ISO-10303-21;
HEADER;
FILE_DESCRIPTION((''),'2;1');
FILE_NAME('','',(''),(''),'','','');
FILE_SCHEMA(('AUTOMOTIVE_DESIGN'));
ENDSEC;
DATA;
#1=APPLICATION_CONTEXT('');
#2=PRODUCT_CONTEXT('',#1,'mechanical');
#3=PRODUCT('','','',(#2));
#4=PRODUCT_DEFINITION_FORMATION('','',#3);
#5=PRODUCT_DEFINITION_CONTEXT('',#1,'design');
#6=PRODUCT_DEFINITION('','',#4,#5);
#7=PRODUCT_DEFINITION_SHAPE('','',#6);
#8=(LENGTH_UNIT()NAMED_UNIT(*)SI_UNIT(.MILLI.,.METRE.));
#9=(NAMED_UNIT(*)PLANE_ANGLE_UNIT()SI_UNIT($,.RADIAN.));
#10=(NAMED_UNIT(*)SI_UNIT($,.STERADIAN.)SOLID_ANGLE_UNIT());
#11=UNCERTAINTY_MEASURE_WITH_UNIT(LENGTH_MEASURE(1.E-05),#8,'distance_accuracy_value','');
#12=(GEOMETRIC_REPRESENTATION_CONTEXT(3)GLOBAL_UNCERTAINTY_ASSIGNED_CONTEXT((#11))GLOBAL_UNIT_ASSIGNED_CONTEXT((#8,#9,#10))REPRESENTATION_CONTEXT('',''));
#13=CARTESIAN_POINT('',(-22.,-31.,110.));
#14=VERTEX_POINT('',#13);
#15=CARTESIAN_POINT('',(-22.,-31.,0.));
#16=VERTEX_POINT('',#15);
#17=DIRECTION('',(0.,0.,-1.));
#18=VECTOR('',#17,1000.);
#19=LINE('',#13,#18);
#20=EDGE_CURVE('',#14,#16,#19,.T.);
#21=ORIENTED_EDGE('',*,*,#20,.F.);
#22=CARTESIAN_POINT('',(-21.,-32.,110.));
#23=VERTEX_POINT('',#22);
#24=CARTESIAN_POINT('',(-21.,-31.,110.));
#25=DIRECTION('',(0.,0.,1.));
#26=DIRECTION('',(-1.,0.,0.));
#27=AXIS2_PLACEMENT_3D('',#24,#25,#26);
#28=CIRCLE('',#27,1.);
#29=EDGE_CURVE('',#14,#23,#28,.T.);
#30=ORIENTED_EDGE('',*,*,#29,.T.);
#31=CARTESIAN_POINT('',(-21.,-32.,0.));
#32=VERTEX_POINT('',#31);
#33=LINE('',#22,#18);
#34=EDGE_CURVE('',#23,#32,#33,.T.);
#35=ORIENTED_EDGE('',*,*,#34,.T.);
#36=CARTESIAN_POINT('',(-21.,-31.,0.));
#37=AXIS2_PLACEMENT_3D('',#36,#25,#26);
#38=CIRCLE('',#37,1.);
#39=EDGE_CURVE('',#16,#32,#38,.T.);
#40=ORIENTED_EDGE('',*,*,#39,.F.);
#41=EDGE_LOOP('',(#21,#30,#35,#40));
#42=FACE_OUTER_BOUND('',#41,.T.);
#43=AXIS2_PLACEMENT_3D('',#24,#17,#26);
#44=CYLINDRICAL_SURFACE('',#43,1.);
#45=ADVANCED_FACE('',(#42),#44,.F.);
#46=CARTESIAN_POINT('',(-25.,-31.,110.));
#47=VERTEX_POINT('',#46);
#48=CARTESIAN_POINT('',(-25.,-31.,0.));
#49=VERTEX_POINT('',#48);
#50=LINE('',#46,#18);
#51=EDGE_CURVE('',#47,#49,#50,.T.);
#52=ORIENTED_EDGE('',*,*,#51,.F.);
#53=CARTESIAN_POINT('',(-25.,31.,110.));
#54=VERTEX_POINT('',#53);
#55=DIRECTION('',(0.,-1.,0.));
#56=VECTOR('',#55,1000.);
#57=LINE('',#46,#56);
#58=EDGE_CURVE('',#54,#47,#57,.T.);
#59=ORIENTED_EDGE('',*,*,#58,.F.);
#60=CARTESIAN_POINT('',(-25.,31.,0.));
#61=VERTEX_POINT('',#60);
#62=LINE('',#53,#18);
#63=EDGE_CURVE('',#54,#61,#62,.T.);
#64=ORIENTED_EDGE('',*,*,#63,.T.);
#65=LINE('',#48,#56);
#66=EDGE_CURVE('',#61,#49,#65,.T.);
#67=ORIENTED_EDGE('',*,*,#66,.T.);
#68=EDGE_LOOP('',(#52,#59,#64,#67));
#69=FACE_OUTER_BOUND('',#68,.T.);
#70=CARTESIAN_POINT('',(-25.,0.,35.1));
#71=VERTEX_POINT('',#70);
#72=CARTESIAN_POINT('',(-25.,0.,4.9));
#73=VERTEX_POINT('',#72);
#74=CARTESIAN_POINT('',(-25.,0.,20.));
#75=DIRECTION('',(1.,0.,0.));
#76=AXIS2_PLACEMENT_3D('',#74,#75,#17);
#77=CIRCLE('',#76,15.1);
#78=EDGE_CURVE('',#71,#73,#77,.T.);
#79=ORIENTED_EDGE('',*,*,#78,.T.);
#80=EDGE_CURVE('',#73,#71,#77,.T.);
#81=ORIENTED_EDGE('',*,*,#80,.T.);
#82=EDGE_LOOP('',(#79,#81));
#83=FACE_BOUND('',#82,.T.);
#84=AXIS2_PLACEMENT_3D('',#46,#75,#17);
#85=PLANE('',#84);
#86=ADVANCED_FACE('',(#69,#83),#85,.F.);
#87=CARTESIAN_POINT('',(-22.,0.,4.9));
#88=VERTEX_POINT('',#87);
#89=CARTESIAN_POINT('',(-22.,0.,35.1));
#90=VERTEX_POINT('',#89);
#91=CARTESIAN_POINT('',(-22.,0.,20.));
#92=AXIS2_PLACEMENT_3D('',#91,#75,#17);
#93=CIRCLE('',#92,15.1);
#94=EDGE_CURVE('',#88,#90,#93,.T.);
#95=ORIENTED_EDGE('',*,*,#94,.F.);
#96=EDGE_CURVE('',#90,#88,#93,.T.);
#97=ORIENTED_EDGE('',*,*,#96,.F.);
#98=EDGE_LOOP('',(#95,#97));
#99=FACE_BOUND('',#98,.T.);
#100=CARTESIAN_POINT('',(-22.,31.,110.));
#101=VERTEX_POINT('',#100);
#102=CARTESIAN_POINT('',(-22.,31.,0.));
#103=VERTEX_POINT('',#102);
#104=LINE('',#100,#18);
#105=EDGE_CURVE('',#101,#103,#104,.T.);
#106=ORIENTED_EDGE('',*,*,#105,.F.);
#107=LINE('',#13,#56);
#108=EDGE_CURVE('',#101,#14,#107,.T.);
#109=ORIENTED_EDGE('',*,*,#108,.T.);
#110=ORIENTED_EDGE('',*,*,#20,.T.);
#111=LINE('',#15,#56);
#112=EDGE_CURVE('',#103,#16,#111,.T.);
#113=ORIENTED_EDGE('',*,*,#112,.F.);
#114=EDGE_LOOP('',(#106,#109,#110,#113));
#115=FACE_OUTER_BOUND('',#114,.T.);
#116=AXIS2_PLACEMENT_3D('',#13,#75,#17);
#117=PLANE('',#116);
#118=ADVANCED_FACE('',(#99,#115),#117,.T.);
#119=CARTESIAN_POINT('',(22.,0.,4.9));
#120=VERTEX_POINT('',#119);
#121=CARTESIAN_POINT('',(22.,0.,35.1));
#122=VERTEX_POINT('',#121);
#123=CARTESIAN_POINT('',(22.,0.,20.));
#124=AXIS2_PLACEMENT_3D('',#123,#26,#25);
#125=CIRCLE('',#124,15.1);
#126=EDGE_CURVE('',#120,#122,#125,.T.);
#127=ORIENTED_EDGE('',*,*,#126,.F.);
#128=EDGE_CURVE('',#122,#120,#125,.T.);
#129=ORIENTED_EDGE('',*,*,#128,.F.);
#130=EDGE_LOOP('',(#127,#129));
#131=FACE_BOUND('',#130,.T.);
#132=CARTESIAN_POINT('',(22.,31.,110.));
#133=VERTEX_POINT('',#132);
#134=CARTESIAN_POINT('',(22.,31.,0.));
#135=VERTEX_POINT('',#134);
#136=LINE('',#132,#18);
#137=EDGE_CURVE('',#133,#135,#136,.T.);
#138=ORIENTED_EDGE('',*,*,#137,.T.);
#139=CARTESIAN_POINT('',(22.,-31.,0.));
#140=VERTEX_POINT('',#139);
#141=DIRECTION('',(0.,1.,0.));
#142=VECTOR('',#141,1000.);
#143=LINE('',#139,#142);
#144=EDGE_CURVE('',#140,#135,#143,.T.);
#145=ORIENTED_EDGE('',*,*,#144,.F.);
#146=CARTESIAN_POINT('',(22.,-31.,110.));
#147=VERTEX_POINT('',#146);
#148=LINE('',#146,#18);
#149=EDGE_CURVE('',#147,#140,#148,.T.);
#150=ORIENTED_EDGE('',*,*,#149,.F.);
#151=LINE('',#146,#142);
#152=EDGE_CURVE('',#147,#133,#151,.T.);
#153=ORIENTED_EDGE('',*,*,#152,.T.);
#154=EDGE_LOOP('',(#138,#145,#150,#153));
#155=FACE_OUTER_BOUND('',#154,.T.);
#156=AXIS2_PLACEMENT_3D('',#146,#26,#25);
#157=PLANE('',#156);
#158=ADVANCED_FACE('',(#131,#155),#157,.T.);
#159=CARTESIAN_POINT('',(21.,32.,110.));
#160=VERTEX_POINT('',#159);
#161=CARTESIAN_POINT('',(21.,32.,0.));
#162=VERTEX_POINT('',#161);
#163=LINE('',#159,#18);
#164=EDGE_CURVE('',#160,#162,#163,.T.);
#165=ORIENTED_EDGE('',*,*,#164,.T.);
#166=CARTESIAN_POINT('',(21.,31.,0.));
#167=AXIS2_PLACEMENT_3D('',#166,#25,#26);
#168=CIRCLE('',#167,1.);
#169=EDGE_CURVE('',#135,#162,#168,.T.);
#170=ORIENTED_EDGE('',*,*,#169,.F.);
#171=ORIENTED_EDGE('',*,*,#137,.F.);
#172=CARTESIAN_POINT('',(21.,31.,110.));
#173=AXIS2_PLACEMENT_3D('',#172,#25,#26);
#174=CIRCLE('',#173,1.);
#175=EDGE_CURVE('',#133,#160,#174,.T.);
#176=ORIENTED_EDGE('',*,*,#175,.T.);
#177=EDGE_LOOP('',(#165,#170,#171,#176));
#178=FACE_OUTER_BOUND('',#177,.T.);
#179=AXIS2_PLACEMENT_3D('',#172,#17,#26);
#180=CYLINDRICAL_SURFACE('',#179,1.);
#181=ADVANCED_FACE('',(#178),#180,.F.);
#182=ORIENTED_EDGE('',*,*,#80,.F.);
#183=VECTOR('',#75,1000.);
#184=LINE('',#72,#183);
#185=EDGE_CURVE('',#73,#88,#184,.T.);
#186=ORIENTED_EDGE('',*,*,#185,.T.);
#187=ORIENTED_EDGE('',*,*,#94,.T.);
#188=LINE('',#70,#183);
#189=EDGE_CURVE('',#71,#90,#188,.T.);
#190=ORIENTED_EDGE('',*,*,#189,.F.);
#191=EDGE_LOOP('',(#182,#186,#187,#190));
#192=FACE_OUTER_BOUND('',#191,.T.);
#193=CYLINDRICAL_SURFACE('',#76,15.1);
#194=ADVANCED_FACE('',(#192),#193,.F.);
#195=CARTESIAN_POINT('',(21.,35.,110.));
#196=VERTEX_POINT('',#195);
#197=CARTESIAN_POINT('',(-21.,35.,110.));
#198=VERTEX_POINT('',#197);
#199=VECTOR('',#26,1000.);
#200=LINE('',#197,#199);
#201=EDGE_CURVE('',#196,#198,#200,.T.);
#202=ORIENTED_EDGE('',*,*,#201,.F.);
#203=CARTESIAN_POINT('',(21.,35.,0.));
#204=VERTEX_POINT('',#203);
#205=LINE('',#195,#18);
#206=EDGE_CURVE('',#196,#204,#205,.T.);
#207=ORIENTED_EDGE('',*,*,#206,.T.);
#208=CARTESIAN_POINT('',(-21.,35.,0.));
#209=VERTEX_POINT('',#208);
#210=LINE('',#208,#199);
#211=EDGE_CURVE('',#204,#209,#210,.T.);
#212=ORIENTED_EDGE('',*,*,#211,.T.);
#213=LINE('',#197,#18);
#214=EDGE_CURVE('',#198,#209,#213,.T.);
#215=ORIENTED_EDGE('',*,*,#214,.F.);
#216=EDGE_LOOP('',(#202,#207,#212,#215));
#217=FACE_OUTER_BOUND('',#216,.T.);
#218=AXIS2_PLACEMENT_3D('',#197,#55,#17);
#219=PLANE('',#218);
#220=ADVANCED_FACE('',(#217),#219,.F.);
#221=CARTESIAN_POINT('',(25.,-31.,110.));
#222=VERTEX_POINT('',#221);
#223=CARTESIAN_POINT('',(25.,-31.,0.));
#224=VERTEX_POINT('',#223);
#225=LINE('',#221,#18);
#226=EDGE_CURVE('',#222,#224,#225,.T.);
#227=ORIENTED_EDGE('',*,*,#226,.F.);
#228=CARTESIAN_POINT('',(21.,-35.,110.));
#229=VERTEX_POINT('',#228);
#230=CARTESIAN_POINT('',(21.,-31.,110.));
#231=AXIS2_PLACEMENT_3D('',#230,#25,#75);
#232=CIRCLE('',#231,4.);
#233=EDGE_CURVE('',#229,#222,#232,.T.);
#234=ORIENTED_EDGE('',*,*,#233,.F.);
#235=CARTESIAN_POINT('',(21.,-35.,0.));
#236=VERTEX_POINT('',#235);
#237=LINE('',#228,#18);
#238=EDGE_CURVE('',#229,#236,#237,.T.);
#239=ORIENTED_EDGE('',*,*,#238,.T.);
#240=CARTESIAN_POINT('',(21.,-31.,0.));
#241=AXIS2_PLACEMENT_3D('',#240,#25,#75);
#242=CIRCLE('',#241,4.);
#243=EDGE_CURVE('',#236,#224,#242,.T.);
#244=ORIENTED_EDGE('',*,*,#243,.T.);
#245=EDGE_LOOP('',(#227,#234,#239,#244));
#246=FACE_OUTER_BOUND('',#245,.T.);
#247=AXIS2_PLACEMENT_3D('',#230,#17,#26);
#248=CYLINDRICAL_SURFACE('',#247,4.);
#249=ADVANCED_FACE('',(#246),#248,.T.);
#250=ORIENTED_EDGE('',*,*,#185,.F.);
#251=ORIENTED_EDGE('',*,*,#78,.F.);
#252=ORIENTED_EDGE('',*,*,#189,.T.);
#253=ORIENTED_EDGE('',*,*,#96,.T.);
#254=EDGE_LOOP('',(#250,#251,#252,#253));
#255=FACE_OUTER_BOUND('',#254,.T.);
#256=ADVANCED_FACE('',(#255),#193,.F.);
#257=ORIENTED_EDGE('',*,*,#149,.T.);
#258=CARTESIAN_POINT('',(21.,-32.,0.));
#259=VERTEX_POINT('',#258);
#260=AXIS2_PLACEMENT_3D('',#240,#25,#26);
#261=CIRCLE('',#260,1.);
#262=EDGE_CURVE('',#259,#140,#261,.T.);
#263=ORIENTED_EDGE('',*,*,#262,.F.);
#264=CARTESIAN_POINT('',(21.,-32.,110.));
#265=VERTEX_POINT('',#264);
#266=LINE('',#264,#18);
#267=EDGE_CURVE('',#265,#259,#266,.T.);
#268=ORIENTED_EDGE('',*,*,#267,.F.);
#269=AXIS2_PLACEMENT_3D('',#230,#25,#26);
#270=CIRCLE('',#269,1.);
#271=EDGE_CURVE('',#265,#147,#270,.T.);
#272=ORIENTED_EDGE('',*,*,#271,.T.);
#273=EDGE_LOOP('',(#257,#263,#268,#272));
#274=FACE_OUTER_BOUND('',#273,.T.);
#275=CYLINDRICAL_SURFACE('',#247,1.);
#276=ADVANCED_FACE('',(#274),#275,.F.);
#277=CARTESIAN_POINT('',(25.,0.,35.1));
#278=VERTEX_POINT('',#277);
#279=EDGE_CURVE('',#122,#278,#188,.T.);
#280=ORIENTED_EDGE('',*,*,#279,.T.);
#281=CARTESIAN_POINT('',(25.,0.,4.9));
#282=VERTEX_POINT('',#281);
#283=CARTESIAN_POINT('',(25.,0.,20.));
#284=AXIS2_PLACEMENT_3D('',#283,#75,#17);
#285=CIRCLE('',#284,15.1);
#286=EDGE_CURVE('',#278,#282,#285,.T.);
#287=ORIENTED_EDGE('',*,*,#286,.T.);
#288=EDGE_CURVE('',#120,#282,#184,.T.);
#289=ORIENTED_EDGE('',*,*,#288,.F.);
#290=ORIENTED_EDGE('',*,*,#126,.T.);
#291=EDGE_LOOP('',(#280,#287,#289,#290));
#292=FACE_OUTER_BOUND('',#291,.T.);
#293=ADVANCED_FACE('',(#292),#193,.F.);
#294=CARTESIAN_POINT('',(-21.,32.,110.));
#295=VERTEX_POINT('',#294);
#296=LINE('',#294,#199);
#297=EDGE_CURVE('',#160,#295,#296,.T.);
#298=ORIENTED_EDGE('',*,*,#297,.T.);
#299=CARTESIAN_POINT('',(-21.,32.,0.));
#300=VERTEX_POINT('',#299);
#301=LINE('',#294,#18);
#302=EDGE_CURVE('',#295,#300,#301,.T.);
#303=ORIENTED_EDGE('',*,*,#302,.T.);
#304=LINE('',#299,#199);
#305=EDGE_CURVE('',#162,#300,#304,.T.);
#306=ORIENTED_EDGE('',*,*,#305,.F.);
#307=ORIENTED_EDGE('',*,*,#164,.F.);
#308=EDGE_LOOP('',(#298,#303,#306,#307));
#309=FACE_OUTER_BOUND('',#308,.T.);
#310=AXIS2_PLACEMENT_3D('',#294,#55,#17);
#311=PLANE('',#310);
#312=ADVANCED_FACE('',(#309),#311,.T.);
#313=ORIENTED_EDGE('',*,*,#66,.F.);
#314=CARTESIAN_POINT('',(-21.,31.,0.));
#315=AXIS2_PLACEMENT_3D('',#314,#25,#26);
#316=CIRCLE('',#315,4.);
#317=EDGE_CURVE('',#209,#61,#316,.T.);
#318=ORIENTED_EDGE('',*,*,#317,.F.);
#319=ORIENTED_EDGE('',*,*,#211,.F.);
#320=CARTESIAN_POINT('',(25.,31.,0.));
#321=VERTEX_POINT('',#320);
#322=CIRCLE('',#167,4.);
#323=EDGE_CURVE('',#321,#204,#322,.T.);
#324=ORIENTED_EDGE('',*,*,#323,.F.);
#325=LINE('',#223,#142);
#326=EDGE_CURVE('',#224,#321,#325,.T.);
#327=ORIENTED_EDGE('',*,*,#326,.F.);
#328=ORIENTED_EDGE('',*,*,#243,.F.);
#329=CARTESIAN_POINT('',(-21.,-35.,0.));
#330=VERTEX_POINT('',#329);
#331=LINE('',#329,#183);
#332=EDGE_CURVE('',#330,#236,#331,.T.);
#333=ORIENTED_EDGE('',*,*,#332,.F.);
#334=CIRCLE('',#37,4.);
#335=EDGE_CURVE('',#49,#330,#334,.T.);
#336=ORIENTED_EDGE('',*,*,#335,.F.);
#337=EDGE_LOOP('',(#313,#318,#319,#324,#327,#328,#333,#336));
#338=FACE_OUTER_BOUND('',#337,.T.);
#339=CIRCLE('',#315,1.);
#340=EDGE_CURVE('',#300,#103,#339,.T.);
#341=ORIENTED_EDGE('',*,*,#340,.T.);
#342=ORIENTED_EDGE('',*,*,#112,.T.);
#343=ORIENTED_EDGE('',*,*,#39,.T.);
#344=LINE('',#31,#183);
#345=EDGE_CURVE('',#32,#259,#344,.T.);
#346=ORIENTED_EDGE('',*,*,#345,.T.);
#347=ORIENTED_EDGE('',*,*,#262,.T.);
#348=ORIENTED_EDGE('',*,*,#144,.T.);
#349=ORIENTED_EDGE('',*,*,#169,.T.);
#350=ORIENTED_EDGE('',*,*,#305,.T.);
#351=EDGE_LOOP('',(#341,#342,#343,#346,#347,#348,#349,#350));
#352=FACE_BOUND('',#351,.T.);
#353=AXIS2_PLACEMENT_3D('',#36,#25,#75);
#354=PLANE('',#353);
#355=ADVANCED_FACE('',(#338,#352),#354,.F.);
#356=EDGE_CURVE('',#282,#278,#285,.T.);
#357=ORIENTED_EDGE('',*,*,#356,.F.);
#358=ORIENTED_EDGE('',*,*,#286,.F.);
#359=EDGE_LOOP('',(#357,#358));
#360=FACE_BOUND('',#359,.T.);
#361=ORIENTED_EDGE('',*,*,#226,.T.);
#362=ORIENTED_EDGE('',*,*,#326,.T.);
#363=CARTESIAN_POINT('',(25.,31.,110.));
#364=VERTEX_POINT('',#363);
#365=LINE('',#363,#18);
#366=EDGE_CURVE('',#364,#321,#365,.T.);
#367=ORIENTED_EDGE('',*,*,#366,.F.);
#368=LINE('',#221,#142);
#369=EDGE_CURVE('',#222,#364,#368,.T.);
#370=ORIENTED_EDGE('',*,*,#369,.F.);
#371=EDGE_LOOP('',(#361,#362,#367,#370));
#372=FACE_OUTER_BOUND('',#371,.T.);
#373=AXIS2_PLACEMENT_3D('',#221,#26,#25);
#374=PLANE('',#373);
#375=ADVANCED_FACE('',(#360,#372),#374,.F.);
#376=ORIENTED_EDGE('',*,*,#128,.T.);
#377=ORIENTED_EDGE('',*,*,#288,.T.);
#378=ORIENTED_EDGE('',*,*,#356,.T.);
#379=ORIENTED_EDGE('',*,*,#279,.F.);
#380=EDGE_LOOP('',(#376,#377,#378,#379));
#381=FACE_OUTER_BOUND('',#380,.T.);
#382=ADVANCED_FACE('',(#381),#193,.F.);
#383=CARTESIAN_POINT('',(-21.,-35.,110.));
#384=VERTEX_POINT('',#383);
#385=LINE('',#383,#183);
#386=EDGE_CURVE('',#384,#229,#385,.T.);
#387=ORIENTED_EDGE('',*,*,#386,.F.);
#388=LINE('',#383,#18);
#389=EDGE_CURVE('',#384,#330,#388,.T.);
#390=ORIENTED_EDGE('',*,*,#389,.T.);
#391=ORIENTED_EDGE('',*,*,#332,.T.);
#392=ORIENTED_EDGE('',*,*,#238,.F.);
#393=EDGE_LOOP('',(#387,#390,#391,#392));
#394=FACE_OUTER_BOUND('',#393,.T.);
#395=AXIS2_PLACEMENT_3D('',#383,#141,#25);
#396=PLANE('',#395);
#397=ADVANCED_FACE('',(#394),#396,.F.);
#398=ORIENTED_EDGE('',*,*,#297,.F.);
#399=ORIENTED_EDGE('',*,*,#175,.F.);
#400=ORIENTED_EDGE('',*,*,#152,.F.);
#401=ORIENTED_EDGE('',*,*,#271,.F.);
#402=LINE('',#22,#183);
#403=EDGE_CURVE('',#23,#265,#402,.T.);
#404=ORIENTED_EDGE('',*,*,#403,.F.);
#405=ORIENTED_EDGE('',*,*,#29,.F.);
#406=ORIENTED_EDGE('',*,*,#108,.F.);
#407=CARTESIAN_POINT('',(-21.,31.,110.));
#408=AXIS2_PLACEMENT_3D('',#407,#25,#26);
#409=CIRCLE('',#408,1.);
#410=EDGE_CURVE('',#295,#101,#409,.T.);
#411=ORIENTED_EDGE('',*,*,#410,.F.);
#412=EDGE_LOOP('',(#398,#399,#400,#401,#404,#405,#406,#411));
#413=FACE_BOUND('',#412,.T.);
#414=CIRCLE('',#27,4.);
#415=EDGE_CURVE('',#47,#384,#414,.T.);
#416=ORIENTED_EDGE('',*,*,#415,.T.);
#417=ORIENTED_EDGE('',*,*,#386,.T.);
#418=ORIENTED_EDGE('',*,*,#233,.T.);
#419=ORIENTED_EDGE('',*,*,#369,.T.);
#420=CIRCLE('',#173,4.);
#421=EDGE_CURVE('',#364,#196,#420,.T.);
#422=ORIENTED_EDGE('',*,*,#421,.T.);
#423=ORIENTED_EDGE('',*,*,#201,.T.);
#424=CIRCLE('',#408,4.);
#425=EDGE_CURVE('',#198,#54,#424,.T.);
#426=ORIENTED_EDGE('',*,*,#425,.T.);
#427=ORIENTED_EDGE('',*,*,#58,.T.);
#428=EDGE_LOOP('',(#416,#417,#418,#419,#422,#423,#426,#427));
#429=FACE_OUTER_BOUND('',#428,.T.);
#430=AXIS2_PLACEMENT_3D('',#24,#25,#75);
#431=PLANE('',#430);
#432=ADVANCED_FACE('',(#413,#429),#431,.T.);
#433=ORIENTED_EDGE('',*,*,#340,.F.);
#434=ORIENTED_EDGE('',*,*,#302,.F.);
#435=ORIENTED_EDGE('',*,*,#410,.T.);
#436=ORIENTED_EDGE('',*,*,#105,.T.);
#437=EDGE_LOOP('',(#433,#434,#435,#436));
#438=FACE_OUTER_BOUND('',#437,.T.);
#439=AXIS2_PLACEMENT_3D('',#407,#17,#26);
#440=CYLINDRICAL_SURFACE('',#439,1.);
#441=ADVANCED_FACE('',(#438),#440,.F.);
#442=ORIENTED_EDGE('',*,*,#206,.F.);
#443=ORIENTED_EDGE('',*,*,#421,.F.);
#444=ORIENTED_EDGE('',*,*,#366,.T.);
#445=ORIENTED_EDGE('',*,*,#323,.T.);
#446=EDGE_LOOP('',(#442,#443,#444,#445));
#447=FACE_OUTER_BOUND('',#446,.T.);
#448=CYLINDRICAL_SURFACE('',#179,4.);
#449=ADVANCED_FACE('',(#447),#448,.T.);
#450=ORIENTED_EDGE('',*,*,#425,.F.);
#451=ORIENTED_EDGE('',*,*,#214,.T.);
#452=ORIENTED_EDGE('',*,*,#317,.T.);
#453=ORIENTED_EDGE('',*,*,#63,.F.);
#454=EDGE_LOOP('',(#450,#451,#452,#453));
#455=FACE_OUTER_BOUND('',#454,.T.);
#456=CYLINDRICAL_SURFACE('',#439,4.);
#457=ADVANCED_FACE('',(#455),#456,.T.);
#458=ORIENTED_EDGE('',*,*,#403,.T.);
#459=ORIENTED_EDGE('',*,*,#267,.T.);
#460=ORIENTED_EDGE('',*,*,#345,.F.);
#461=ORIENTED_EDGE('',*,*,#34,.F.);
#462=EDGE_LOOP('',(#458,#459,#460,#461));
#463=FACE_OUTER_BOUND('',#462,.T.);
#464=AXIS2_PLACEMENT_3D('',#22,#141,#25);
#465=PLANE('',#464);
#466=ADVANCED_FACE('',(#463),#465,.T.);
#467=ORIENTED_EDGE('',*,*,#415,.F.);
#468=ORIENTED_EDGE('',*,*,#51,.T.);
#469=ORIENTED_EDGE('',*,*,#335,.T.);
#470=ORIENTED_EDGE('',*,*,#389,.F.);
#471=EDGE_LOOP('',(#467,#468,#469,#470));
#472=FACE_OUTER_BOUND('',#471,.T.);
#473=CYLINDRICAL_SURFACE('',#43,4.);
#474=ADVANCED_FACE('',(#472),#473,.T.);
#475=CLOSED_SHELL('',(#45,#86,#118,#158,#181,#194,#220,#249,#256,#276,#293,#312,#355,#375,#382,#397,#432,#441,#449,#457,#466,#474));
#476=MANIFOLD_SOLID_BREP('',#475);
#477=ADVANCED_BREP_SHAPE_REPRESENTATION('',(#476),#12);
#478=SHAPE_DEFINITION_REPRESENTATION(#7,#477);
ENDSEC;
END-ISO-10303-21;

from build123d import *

# Parameters (mm, degrees)
EXTRUDE_THIN1_DEPTH = 110
SKETCH2_R           = 15.1
CUT_EXTRUDE1_DEPTH  = 126.797456254


with BuildPart() as part:
    # Sketch1 → Extrude-Thin1 (new body)
    with BuildSketch(Plane.XY):
        with BuildLine():
            Line((-25, 31), (-25, -31))
            ThreePointArc((-25, -31), (-23.828427125, -33.828427125), (-21, -35))
            Line((-21, -35), (21, -35))
            ThreePointArc((21, -35), (23.828427125, -33.828427125), (25, -31))
            Line((25, -31), (25, 31))
            ThreePointArc((25, 31), (23.828427125, 33.828427125), (21, 35))
            Line((21, 35), (-21, 35))
            ThreePointArc((-21, 35), (-23.828427125, 33.828427125), (-25, 31))
        make_face()
        with BuildLine():
            Line((-22, 31), (-22, -31))
            ThreePointArc((-22, -31), (-21.707106781, -31.707106781), (-21, -32))
            Line((-21, -32), (21, -32))
            ThreePointArc((21, -32), (21.707106781, -31.707106781), (22, -31))
            Line((22, -31), (22, 31))
            ThreePointArc((22, 31), (21.707106781, 31.707106781), (21, 32))
            Line((21, 32), (-21, 32))
            ThreePointArc((-21, 32), (-21.707106781, 31.707106781), (-22, 31))
        make_face(mode=Mode.SUBTRACT)
    extrude(amount=EXTRUDE_THIN1_DEPTH)

    # Sketch2 → Cut-Extrude1 (cut, through all)
    with BuildSketch(Plane(origin=(25, 0, 0), x_dir=(0, 0, -1), z_dir=(1, 0, 0))):
        with Locations((-20, 0)):
            Circle(SKETCH2_R)
    extrude(amount=-CUT_EXTRUDE1_DEPTH, mode=Mode.SUBTRACT)


solid = part.part
